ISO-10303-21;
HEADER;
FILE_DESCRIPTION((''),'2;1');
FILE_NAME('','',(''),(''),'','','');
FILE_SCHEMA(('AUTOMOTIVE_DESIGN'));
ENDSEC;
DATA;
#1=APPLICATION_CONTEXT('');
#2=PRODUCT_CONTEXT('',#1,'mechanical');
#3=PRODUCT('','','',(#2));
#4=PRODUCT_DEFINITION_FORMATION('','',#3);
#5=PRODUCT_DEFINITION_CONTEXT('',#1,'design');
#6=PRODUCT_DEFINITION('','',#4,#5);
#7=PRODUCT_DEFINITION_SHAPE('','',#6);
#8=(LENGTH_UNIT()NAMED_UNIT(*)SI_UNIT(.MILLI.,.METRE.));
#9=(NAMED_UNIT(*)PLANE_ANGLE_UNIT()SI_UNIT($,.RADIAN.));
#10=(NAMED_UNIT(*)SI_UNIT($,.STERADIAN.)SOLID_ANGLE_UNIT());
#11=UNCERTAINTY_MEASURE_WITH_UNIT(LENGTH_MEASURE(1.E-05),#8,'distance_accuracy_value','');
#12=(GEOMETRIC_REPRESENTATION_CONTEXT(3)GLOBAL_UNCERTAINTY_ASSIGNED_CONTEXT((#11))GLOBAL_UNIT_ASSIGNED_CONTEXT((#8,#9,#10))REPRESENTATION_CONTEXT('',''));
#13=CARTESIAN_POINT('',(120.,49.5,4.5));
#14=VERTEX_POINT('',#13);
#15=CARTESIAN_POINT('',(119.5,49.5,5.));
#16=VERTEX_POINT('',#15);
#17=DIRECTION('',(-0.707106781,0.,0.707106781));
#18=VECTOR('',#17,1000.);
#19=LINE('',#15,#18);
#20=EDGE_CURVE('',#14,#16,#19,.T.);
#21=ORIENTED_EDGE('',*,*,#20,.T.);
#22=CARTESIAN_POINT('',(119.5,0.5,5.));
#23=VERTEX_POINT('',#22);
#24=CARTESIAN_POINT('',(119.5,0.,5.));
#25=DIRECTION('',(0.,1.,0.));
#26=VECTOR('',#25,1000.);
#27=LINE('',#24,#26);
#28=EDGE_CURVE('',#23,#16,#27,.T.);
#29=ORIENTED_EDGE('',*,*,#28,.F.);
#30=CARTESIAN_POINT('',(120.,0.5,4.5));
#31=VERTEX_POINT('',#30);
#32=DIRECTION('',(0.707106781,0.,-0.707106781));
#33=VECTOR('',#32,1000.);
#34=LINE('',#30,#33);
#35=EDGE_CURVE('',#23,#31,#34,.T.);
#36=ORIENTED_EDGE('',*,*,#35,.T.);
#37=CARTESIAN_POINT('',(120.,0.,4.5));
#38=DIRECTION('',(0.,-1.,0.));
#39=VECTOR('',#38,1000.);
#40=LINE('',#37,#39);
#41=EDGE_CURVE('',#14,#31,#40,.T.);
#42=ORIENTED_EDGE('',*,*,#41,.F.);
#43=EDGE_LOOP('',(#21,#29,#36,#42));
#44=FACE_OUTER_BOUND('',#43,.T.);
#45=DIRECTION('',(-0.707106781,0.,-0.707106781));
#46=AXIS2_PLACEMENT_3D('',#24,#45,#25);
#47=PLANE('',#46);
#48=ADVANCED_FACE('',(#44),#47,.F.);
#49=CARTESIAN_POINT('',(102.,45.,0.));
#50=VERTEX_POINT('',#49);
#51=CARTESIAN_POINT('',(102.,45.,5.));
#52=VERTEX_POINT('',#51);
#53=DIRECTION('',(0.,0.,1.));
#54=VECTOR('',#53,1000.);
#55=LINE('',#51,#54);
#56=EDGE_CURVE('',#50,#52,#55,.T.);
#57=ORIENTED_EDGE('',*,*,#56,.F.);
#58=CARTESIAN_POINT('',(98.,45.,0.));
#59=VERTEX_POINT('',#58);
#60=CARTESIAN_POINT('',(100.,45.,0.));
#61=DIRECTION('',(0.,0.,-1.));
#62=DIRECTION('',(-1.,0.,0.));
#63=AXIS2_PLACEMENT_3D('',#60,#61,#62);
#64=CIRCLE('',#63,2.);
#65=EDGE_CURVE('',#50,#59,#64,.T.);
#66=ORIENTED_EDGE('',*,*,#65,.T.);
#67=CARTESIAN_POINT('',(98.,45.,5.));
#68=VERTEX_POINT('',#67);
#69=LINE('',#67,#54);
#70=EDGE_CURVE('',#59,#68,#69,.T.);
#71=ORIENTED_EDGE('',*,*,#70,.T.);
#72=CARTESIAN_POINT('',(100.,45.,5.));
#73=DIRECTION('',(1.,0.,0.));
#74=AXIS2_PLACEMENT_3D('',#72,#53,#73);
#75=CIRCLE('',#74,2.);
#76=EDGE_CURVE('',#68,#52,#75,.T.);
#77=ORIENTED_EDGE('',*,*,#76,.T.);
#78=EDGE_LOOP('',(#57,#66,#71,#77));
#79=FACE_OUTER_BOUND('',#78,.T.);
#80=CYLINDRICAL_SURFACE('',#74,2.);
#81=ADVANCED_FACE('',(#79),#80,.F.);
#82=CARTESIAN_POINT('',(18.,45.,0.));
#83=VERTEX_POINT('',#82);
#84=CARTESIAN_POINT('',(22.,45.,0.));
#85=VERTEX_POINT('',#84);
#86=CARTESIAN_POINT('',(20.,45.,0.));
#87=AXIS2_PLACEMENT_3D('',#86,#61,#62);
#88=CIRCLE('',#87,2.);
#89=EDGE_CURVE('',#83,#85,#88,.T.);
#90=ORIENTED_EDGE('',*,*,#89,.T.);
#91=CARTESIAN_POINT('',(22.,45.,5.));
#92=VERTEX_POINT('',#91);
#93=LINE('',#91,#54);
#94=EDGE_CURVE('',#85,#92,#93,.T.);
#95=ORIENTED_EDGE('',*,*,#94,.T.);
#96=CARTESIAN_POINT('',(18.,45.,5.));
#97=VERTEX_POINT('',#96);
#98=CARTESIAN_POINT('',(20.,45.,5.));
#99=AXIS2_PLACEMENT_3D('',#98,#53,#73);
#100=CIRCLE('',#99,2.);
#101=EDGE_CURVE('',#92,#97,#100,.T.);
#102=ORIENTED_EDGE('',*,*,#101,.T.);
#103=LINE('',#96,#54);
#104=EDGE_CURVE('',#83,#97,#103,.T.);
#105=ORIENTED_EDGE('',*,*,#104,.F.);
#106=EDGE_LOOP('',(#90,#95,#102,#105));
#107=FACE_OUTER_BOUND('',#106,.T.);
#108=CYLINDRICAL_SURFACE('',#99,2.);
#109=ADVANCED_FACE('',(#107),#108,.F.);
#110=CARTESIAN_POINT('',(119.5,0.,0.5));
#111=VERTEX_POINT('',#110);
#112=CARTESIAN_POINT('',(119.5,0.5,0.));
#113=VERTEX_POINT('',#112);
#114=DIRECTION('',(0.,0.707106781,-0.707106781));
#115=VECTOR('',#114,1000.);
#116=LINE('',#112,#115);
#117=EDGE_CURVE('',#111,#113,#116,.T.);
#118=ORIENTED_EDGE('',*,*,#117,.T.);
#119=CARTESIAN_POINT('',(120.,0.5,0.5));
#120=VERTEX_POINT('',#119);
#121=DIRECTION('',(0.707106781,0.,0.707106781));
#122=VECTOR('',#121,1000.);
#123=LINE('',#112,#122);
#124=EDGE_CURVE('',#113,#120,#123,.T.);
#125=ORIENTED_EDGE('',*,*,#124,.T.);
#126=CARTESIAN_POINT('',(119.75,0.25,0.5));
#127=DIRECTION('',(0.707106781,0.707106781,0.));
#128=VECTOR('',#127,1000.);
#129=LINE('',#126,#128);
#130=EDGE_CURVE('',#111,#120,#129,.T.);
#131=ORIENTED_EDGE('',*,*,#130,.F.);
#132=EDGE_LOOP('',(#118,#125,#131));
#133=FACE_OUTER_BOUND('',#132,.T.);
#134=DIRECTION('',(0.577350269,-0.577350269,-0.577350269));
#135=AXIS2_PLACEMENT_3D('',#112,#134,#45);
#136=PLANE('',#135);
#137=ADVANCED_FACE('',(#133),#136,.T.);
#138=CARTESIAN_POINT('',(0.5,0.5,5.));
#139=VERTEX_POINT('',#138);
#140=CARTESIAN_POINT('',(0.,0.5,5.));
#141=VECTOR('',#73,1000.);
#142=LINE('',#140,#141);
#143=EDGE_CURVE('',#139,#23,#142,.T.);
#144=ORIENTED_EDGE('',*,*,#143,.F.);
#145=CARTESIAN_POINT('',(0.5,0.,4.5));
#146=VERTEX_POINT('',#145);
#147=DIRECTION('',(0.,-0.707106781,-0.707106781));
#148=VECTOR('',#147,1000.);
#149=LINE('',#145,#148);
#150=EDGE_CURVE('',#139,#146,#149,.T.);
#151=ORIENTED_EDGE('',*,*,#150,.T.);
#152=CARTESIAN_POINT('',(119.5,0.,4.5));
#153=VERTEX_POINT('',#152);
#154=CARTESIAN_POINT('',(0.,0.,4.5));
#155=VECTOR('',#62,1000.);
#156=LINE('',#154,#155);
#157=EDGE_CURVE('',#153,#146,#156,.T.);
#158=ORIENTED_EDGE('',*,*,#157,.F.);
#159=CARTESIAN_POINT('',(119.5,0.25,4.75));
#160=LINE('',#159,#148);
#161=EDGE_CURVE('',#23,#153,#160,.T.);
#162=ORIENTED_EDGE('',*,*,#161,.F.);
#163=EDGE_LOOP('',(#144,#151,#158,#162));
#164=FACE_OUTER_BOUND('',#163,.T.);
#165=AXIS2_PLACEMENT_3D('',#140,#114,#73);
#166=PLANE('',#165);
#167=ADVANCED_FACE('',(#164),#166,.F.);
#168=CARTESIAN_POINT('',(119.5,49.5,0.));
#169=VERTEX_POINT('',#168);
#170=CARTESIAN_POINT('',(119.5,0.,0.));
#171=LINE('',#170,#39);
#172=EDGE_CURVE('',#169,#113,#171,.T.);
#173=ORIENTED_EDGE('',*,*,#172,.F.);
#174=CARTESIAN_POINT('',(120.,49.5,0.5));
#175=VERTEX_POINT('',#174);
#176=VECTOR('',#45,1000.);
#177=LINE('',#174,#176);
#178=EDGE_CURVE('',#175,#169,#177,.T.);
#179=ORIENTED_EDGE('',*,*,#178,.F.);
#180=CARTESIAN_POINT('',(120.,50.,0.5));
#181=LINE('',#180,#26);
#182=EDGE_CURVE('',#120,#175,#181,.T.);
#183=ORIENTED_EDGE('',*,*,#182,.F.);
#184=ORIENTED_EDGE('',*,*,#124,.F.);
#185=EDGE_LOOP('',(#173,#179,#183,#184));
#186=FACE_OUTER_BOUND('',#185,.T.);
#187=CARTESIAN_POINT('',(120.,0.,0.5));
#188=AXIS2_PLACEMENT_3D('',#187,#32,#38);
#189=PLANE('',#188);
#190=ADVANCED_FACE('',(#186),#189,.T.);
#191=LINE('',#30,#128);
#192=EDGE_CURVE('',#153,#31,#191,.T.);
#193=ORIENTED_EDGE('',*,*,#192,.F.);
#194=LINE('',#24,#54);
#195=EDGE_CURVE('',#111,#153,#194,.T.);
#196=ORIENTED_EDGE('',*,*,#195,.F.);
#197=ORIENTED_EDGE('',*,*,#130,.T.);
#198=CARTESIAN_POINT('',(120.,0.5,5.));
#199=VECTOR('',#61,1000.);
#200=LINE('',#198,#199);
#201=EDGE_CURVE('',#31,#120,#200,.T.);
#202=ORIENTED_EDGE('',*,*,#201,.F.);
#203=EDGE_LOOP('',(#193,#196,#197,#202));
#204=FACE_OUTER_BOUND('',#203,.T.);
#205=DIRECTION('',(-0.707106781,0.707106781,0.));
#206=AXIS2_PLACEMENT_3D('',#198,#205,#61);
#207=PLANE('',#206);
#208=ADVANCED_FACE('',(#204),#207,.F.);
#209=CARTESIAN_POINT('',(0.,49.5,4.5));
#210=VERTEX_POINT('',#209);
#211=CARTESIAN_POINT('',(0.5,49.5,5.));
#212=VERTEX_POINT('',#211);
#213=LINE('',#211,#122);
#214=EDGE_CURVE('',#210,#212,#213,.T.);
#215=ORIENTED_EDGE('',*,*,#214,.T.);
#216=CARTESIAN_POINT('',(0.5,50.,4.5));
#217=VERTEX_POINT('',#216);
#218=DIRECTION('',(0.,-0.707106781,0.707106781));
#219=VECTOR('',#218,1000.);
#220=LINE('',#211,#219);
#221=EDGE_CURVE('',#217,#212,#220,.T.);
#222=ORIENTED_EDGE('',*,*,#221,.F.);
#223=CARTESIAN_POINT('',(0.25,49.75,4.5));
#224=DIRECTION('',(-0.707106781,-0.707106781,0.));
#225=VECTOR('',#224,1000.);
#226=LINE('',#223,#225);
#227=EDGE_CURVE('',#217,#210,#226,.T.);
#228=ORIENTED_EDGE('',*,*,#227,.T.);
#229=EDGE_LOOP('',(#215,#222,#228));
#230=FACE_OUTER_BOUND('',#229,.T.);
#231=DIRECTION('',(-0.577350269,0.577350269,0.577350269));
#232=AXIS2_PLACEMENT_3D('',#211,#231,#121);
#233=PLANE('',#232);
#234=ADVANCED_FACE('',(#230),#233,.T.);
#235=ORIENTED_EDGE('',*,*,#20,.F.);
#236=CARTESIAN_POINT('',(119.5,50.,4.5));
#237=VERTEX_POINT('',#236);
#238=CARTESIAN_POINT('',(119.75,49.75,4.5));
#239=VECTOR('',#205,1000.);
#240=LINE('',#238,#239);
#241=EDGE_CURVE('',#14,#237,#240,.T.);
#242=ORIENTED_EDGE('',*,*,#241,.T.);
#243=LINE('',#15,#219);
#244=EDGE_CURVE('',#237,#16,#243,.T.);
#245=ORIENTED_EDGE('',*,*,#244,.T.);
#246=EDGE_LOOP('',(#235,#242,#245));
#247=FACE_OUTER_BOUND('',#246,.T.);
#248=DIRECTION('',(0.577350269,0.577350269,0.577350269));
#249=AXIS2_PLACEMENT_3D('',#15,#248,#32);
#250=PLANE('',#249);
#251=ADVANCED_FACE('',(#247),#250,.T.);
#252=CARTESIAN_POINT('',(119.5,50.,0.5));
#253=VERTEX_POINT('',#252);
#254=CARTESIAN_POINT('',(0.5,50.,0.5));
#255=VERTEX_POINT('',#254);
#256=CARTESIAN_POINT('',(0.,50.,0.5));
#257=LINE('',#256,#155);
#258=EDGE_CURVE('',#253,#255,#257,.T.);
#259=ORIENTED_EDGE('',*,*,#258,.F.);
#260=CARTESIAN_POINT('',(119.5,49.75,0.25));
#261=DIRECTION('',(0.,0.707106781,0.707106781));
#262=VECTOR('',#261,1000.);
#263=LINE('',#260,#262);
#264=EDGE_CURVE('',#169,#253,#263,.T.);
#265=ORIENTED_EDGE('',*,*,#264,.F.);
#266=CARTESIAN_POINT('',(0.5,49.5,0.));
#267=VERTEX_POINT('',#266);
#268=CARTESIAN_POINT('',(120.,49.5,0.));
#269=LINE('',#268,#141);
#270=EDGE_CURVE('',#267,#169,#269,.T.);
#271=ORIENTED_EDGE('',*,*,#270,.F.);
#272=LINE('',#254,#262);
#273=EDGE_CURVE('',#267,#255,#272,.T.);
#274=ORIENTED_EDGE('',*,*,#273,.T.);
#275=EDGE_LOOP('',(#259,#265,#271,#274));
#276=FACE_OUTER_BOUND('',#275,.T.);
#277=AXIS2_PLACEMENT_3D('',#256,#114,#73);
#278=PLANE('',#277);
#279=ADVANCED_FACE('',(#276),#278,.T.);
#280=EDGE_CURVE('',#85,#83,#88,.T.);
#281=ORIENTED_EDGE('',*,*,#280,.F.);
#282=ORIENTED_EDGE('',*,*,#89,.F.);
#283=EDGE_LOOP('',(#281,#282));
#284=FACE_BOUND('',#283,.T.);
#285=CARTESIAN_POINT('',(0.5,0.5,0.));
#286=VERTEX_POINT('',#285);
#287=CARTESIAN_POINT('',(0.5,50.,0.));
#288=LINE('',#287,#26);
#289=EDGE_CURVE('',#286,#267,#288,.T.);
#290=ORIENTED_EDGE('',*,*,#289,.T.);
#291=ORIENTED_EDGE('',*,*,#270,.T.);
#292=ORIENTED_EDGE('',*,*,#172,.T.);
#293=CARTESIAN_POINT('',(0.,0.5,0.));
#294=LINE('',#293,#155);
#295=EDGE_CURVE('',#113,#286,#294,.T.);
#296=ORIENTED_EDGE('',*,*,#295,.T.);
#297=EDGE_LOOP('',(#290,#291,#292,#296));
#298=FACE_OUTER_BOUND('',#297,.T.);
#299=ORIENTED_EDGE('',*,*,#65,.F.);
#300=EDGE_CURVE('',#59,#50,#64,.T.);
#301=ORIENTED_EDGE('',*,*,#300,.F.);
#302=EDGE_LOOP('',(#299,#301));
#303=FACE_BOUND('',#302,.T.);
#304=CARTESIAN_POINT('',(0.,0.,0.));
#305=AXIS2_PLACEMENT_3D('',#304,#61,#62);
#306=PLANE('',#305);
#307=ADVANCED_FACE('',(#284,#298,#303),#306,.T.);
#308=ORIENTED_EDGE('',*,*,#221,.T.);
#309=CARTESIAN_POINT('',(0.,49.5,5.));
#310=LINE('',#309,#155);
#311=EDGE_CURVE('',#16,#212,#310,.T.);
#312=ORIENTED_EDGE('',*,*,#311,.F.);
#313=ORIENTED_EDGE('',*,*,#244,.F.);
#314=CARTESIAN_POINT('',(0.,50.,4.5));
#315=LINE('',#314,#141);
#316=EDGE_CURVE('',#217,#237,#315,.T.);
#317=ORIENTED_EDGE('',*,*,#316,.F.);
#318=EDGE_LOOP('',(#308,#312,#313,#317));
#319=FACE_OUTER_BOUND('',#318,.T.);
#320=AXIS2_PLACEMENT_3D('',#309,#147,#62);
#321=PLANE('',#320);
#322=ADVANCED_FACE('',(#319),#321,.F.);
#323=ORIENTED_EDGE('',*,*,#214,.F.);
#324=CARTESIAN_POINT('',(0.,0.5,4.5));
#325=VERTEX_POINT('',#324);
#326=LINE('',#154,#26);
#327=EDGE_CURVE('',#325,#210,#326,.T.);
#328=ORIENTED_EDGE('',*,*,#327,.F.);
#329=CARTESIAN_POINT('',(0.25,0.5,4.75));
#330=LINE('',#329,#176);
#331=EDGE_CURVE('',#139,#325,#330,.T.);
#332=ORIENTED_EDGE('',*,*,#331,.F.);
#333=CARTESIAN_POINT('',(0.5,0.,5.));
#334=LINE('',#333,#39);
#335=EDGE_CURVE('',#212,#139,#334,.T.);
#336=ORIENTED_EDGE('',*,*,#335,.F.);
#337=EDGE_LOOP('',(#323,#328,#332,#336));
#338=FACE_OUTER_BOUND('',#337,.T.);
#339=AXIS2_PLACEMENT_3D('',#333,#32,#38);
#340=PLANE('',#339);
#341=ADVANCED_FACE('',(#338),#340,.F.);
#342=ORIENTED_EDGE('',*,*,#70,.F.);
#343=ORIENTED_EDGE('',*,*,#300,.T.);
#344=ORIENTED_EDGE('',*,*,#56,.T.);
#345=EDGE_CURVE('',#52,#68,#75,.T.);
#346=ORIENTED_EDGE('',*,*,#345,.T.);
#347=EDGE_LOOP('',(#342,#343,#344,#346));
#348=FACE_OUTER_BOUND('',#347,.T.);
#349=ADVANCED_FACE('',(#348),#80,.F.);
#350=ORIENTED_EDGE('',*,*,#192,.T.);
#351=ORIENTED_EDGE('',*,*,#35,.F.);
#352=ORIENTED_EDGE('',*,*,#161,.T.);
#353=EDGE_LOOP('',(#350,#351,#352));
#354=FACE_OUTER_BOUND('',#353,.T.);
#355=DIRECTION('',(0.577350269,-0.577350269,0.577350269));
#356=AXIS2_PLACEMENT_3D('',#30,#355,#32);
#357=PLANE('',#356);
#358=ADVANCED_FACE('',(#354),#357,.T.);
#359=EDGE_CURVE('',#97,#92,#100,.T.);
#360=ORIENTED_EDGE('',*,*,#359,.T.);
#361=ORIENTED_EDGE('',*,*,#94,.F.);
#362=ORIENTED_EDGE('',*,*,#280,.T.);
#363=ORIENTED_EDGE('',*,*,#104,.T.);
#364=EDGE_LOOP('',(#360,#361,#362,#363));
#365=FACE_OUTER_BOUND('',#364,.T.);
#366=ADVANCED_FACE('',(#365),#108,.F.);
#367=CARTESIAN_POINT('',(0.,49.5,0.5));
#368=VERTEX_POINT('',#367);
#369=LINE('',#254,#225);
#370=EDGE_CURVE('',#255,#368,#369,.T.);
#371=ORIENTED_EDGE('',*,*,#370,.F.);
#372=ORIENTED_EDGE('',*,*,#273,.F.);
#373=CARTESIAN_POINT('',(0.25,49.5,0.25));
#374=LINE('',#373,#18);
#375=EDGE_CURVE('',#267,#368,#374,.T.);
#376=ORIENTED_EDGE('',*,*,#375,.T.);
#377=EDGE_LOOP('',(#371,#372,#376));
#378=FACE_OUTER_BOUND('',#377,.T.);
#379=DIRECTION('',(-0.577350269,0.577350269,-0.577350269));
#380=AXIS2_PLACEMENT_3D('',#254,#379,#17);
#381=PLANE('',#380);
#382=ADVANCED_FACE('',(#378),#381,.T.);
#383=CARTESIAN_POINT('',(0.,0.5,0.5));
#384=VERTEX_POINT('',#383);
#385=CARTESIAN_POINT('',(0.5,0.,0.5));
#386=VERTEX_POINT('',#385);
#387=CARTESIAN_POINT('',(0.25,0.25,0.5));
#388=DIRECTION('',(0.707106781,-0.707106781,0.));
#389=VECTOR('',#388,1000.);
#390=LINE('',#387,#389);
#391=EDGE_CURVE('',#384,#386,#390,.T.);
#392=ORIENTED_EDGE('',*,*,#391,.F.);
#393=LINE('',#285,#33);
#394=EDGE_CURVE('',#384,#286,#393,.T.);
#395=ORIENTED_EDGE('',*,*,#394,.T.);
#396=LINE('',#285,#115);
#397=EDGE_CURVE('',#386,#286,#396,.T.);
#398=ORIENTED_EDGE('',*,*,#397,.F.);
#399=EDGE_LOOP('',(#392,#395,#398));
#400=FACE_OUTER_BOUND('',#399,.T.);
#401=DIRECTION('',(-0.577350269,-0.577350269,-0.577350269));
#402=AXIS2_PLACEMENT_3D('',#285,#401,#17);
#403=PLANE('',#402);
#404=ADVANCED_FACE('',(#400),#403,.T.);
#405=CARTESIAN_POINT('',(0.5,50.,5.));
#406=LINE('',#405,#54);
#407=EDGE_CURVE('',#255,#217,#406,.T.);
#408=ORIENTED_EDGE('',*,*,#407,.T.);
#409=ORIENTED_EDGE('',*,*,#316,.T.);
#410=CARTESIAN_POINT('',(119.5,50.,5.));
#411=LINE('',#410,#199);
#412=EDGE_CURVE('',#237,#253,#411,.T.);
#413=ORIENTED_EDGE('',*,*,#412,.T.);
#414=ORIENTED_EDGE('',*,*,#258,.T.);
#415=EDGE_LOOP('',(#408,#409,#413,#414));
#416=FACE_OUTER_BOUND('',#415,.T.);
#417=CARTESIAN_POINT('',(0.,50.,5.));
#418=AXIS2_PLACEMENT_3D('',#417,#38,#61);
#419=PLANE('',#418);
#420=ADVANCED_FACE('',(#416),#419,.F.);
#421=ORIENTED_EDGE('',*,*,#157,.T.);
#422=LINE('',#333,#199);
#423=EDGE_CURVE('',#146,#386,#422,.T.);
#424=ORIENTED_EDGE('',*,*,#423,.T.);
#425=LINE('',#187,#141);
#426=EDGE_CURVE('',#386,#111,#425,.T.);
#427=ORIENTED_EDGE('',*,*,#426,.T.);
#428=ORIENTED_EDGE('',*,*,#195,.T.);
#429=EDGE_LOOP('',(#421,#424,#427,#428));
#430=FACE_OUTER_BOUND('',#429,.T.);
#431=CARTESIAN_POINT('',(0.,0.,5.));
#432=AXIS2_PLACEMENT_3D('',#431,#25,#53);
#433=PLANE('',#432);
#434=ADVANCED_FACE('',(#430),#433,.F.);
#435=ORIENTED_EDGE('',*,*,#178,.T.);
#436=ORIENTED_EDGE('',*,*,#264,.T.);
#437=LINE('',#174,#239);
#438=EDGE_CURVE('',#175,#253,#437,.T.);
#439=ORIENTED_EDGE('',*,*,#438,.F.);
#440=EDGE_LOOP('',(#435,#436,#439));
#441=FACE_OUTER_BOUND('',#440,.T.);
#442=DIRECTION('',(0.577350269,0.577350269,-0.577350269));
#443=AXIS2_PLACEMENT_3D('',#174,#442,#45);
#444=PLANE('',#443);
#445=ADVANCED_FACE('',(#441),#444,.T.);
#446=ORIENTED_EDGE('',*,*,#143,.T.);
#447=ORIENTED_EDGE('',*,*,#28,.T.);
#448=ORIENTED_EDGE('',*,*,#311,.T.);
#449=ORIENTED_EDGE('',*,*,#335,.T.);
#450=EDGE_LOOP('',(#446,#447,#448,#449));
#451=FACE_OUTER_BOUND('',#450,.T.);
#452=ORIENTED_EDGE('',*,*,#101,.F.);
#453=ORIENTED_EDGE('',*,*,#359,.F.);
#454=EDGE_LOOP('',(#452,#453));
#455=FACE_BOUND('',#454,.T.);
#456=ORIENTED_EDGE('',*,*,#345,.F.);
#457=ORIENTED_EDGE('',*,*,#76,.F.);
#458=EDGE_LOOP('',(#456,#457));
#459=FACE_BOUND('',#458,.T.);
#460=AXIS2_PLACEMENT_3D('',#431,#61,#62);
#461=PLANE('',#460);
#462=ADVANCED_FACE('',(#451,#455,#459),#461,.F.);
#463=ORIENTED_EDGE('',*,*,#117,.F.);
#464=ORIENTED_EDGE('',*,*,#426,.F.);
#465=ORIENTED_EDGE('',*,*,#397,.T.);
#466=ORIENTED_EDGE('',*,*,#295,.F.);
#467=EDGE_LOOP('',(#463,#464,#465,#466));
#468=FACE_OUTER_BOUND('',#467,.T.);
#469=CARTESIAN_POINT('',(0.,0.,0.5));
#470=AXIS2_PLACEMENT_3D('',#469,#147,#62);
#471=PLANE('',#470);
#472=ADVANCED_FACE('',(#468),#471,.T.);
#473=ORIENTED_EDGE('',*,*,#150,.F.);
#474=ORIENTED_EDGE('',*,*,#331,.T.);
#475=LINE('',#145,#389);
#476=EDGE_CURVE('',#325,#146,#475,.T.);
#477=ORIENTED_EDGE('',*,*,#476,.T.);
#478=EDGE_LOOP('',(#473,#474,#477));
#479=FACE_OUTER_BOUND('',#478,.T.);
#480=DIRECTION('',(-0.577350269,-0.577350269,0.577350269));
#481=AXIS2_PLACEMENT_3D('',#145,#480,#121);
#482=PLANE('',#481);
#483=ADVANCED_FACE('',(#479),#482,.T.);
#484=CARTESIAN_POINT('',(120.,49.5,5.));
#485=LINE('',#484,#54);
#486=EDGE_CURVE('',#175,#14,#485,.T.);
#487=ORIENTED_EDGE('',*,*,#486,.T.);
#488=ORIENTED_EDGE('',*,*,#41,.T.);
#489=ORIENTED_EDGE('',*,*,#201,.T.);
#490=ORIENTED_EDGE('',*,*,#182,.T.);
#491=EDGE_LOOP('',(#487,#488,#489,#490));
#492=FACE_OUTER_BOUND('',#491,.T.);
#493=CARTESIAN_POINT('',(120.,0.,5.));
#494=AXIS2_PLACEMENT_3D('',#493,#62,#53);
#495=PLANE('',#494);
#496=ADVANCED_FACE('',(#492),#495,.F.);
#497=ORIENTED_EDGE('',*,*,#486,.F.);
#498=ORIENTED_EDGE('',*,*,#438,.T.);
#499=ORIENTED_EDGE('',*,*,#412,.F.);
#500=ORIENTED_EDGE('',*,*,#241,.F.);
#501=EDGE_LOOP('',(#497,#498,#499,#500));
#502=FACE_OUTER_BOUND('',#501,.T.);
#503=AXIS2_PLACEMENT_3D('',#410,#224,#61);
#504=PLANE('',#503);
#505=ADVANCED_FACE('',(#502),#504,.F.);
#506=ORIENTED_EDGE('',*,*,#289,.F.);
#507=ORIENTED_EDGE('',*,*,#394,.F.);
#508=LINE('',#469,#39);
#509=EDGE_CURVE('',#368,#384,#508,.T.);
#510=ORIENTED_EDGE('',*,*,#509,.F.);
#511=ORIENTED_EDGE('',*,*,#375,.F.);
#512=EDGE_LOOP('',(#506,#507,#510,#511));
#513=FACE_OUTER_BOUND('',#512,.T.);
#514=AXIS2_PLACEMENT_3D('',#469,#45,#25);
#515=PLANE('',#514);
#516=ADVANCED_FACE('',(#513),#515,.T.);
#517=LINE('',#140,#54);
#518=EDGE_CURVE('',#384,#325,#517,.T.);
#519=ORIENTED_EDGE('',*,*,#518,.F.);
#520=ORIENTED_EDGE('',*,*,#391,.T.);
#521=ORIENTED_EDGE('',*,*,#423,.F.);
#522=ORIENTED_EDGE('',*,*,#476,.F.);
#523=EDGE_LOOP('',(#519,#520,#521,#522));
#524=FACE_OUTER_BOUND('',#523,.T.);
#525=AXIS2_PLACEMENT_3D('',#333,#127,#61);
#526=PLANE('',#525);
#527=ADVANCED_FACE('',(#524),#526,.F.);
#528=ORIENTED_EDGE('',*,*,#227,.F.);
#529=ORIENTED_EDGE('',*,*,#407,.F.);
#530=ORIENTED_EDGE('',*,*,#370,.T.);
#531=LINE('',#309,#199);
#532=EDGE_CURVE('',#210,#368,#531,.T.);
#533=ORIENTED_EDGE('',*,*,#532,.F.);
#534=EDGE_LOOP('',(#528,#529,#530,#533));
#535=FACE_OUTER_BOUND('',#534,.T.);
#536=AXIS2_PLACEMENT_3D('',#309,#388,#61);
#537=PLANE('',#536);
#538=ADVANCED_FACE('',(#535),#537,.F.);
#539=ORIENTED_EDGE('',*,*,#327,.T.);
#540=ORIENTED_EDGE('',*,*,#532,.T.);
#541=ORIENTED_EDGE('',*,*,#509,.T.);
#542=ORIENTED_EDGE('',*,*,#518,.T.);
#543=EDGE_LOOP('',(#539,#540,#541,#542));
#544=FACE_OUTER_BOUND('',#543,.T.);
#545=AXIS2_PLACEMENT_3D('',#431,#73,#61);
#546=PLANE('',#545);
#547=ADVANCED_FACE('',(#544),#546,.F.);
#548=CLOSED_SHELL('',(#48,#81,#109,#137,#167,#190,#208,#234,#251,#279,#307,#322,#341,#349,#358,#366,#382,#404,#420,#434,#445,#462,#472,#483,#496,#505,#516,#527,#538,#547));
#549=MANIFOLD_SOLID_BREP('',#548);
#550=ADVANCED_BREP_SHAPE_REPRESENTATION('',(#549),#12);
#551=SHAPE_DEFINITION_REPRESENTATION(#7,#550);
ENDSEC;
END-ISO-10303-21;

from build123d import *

# Parameters (mm, degrees)
SKETCH1_W                 = 120
SKETCH1_H                 = 50
BOSS_EXTRUDE1_DEPTH       = 5
F_4_0MM_DOWEL_HOLE1_D     = 4
F_4_0MM_DOWEL_HOLE1_DEPTH = 12
F_4_0MM_DOWEL_HOLE1_TIP   = 1.201721238
CHAMFER1_SIZE             = 0.5


with BuildPart() as part:
    # Sketch1 → Boss-Extrude1 (new body)
    with BuildSketch(Plane.XY):
        with Locations((60, 25)):
            Rectangle(SKETCH1_W, SKETCH1_H)
    extrude(amount=BOSS_EXTRUDE1_DEPTH)

    # Ø4.0mm dowel hole1
    with Locations(Plane.XY.offset(5)):
        with Locations((20, 45), (100, 45)):
            Hole(F_4_0MM_DOWEL_HOLE1_D / 2, depth=F_4_0MM_DOWEL_HOLE1_DEPTH)
            with Locations((0, 0, -(F_4_0MM_DOWEL_HOLE1_DEPTH + F_4_0MM_DOWEL_HOLE1_TIP / 2))):  # 118° drill point
                Cone(0, F_4_0MM_DOWEL_HOLE1_D / 2, F_4_0MM_DOWEL_HOLE1_TIP, mode=Mode.SUBTRACT)

    # Chamfer1
    chamfer1_edges = [part.edges().sort_by_distance(p)[0] for p in [
        (120, 25, 5),
        (60, 50, 5),
        (0, 25, 5),
        (60, 50, 0),
        (120, 25, 0),
        (60, 0, 0),
        (0, 25, 0),
        (0, 50, 2.5),
        (120, 50, 2.5),
        (120, 0, 2.5),
        (0, 0, 2.5),
        (60, 0, 5),
    ]]
    chamfer(chamfer1_edges, length=CHAMFER1_SIZE)


solid = part.part
